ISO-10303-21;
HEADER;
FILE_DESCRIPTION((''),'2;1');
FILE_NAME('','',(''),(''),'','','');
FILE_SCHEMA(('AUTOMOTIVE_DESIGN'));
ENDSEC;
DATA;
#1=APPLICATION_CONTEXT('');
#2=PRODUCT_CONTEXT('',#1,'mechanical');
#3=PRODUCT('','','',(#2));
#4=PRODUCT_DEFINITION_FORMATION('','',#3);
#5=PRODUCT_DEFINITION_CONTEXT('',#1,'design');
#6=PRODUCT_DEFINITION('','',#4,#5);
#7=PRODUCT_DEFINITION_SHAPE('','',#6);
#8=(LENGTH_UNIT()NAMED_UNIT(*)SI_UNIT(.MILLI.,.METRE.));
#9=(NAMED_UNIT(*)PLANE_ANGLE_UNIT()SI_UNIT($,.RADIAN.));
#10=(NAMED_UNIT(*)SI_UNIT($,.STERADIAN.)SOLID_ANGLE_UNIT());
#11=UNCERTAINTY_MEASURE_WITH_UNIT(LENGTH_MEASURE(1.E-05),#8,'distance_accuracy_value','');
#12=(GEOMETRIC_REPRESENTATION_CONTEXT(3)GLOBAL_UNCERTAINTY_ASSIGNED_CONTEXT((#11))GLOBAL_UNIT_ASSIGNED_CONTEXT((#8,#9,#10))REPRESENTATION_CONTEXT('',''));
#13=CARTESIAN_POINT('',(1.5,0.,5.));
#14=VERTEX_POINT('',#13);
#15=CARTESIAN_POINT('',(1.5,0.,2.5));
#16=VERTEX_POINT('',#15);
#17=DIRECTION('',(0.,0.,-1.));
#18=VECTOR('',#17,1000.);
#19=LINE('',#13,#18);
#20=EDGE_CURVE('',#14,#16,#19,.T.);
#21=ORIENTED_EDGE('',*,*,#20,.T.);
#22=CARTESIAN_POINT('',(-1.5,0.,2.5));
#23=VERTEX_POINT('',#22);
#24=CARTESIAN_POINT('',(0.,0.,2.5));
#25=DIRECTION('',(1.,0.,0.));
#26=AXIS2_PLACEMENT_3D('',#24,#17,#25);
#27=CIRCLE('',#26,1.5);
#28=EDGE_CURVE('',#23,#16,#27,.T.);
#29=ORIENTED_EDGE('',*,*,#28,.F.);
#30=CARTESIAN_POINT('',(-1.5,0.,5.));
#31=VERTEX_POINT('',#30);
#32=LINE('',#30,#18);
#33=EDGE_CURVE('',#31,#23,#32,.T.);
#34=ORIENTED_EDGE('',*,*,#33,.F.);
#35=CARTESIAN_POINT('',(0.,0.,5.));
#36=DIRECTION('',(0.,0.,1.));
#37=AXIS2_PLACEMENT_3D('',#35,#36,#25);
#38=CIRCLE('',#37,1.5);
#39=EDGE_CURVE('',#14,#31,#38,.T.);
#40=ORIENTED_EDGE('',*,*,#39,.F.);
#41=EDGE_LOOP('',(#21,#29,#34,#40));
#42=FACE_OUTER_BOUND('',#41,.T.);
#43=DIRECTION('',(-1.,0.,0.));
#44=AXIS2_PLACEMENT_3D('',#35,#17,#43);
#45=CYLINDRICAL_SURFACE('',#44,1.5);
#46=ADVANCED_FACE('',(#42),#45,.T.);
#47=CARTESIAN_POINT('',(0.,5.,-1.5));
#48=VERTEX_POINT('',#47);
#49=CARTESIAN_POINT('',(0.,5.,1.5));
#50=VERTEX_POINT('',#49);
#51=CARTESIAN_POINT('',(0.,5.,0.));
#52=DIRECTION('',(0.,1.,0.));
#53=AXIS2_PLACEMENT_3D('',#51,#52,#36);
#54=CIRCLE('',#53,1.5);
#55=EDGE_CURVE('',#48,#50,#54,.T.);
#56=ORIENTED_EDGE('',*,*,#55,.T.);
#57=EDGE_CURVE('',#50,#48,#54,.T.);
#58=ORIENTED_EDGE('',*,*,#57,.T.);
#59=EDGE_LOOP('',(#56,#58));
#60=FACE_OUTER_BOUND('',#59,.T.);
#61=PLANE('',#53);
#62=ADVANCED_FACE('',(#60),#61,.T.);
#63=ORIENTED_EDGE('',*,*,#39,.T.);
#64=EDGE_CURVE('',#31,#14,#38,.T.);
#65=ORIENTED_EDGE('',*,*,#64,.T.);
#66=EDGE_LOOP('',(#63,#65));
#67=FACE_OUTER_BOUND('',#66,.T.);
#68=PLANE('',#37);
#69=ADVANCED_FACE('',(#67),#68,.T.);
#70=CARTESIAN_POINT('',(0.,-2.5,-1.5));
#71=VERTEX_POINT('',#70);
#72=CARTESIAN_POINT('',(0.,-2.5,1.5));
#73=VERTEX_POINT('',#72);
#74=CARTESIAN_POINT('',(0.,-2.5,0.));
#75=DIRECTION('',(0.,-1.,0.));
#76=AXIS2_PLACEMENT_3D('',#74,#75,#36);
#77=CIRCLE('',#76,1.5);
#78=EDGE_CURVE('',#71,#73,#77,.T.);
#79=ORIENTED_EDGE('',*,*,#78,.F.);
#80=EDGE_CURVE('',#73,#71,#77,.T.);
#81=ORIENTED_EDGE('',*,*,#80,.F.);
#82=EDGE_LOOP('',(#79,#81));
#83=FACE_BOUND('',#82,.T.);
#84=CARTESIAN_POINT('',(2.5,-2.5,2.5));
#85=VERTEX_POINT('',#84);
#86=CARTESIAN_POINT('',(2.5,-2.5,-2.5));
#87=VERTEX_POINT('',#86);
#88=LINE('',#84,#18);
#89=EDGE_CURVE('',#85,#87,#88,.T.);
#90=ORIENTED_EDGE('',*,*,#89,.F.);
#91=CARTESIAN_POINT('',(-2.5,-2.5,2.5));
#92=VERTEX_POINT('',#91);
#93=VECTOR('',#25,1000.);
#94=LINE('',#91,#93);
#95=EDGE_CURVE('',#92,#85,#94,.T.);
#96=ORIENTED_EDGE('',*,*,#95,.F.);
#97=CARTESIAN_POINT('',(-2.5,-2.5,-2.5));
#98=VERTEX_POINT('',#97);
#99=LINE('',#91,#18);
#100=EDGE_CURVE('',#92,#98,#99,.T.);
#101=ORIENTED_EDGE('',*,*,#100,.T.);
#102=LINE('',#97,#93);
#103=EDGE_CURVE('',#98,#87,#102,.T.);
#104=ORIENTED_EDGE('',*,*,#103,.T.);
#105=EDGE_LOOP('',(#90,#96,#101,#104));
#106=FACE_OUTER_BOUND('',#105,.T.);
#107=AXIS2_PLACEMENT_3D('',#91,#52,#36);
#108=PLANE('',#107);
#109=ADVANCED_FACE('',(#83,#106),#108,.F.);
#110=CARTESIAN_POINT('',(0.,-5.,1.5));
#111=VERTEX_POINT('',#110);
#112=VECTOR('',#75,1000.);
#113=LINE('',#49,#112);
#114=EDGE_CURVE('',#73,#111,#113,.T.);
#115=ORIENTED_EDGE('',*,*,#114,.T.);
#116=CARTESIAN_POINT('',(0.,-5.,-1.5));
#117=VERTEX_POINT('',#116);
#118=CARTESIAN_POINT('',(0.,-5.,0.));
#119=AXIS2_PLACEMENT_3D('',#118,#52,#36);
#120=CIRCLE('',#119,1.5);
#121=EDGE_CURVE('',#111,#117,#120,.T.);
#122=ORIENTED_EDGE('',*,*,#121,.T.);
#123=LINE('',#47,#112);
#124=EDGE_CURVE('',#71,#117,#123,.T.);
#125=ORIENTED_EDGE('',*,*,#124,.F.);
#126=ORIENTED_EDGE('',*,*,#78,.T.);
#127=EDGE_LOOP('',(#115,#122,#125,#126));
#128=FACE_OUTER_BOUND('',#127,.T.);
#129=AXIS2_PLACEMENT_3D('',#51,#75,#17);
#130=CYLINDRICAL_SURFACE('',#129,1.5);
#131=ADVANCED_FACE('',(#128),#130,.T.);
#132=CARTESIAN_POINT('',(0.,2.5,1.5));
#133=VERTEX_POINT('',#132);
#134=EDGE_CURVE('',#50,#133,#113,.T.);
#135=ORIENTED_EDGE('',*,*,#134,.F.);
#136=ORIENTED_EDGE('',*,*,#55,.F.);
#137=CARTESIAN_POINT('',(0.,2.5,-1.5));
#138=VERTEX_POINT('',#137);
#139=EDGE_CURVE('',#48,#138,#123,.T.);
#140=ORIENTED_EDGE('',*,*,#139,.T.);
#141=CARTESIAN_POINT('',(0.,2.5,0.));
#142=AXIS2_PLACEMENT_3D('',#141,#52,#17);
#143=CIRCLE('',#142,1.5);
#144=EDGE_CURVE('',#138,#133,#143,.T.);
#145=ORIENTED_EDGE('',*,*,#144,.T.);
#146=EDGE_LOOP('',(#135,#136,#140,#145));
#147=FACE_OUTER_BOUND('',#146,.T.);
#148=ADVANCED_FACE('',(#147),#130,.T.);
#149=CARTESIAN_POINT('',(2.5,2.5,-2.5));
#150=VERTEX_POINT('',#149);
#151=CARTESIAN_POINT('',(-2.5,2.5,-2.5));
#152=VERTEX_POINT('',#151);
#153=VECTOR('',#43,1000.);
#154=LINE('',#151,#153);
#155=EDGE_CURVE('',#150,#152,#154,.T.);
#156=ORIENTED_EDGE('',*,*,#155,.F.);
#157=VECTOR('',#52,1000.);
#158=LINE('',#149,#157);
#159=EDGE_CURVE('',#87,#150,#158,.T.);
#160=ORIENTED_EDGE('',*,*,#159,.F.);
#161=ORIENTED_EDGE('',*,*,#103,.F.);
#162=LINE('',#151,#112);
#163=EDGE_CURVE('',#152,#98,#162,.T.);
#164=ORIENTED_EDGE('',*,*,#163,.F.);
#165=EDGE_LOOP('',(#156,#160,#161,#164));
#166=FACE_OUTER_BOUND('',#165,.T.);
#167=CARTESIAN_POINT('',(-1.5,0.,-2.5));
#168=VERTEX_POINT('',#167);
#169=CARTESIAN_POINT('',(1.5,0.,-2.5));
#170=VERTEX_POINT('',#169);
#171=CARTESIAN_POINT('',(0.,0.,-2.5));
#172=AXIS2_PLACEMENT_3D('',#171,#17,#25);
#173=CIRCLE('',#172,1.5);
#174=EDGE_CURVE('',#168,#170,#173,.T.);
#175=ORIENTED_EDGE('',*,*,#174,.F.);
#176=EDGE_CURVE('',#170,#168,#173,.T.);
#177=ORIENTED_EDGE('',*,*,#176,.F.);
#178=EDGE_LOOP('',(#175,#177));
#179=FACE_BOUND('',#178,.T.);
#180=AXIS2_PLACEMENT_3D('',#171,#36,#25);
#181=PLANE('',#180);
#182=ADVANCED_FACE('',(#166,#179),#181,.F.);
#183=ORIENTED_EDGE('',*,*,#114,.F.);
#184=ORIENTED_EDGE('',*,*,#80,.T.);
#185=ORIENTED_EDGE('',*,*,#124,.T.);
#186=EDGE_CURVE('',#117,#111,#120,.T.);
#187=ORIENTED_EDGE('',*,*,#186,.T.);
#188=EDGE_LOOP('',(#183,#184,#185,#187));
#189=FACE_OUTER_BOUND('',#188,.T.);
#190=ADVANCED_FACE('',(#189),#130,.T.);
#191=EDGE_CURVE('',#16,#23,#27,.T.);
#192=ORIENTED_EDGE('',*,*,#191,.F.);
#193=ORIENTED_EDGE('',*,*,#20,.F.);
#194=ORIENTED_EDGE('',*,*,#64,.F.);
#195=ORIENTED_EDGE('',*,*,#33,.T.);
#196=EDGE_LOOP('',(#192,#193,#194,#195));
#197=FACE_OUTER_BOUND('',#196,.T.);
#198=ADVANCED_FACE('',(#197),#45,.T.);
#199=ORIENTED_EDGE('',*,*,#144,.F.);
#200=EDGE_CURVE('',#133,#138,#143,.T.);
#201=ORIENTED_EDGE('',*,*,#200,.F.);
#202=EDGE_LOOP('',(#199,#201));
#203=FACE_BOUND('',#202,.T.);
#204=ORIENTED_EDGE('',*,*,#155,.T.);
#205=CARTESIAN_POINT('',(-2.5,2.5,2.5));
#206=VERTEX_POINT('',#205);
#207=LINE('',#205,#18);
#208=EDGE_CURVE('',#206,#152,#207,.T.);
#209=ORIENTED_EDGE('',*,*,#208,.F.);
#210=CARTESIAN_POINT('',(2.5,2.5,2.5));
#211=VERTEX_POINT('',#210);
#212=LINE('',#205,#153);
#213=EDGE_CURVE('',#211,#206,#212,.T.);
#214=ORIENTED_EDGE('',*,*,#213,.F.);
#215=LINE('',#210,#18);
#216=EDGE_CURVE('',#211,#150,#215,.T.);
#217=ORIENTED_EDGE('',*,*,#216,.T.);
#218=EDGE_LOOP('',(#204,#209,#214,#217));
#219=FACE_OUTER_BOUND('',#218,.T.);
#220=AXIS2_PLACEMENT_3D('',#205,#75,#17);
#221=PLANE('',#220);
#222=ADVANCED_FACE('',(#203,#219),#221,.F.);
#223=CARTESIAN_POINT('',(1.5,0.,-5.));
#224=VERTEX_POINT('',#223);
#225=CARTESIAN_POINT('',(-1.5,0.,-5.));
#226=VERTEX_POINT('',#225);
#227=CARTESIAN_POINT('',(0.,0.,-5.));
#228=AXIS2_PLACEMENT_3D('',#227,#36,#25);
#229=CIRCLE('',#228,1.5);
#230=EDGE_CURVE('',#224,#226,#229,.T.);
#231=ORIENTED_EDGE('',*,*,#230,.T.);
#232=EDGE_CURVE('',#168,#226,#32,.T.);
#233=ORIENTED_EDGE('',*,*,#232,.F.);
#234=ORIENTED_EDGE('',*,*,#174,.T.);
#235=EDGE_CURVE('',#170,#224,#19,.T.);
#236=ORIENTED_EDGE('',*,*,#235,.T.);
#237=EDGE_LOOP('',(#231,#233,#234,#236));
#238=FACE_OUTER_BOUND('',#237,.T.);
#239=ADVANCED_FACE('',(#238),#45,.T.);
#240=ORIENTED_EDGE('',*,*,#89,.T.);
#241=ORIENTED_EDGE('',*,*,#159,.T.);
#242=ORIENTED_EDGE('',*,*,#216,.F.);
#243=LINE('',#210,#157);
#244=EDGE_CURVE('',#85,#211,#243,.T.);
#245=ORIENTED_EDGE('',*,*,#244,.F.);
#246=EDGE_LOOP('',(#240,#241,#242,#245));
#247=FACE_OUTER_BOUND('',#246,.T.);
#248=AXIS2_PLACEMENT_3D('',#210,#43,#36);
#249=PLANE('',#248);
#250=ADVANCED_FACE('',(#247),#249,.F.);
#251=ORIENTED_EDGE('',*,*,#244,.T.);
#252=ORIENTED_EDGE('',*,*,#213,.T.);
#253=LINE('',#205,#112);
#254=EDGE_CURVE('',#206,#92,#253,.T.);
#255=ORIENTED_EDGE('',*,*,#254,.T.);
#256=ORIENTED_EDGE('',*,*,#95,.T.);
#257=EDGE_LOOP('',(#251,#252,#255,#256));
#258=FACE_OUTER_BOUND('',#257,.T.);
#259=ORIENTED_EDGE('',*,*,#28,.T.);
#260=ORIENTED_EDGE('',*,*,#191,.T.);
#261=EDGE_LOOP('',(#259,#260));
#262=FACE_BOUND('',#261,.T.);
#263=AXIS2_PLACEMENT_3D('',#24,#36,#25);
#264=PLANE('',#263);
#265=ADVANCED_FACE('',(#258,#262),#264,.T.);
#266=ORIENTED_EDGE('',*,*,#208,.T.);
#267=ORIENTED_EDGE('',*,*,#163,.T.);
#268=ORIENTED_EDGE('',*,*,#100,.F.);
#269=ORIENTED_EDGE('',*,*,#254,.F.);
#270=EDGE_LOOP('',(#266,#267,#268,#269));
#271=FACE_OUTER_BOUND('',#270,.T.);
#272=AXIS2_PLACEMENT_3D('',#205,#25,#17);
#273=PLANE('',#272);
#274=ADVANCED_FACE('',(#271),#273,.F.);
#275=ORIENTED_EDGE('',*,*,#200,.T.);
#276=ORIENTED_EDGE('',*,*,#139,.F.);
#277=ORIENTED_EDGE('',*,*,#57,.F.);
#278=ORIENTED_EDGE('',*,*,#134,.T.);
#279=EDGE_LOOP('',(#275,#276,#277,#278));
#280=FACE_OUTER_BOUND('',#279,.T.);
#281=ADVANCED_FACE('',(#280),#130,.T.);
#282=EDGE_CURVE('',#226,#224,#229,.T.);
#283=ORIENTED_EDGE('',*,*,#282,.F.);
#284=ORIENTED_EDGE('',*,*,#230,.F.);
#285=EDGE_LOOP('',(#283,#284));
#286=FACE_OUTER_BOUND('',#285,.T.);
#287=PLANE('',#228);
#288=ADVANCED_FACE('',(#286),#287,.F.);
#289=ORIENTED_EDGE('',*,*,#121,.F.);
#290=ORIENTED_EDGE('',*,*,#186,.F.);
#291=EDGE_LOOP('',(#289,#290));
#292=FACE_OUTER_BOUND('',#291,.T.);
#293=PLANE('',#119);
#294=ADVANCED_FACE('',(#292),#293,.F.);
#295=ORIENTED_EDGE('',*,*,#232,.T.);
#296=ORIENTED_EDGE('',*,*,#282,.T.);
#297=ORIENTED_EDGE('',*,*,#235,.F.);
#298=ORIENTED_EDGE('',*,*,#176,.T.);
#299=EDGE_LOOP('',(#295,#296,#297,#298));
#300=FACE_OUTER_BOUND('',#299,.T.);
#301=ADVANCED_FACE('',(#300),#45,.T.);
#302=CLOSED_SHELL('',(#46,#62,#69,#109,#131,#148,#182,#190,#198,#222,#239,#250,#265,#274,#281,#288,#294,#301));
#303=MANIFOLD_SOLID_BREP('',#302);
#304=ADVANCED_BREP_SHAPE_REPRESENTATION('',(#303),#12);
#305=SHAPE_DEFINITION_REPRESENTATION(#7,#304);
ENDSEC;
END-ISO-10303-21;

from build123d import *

# Parameters (mm, degrees)
SKETCH_1_W      = 5
SKETCH_1_H      = 5
EXTRUDE_1_DEPTH = 2.5
SKETCH_2_R      = 1.5
EXTRUDE_2_DEPTH = 5
SKETCH_3_R      = 1.5
EXTRUDE_3_DEPTH = 5


with BuildPart() as part:
    # 草图1 → 凸台-拉伸1 (new, symmetric)
    with BuildSketch(Plane.XY):
        Rectangle(SKETCH_1_W, SKETCH_1_H)
    extrude(amount=EXTRUDE_1_DEPTH, both=True)

    # 草图2 → 凸台-拉伸2 (add, symmetric)
    with BuildSketch(Plane(origin=(0, 0, 0), x_dir=(1, 0, 0), z_dir=(0, 1, 0))):
        with Locations(Location((0, 0, 0), (0, 0, 90))):
            Circle(SKETCH_2_R)
    extrude(amount=EXTRUDE_2_DEPTH, both=True)

    # 草图3 → 凸台-拉伸3 (add, symmetric)
    with BuildSketch(Plane.XY):
        Circle(SKETCH_3_R)
    extrude(amount=EXTRUDE_3_DEPTH, both=True)


solid = part.part
